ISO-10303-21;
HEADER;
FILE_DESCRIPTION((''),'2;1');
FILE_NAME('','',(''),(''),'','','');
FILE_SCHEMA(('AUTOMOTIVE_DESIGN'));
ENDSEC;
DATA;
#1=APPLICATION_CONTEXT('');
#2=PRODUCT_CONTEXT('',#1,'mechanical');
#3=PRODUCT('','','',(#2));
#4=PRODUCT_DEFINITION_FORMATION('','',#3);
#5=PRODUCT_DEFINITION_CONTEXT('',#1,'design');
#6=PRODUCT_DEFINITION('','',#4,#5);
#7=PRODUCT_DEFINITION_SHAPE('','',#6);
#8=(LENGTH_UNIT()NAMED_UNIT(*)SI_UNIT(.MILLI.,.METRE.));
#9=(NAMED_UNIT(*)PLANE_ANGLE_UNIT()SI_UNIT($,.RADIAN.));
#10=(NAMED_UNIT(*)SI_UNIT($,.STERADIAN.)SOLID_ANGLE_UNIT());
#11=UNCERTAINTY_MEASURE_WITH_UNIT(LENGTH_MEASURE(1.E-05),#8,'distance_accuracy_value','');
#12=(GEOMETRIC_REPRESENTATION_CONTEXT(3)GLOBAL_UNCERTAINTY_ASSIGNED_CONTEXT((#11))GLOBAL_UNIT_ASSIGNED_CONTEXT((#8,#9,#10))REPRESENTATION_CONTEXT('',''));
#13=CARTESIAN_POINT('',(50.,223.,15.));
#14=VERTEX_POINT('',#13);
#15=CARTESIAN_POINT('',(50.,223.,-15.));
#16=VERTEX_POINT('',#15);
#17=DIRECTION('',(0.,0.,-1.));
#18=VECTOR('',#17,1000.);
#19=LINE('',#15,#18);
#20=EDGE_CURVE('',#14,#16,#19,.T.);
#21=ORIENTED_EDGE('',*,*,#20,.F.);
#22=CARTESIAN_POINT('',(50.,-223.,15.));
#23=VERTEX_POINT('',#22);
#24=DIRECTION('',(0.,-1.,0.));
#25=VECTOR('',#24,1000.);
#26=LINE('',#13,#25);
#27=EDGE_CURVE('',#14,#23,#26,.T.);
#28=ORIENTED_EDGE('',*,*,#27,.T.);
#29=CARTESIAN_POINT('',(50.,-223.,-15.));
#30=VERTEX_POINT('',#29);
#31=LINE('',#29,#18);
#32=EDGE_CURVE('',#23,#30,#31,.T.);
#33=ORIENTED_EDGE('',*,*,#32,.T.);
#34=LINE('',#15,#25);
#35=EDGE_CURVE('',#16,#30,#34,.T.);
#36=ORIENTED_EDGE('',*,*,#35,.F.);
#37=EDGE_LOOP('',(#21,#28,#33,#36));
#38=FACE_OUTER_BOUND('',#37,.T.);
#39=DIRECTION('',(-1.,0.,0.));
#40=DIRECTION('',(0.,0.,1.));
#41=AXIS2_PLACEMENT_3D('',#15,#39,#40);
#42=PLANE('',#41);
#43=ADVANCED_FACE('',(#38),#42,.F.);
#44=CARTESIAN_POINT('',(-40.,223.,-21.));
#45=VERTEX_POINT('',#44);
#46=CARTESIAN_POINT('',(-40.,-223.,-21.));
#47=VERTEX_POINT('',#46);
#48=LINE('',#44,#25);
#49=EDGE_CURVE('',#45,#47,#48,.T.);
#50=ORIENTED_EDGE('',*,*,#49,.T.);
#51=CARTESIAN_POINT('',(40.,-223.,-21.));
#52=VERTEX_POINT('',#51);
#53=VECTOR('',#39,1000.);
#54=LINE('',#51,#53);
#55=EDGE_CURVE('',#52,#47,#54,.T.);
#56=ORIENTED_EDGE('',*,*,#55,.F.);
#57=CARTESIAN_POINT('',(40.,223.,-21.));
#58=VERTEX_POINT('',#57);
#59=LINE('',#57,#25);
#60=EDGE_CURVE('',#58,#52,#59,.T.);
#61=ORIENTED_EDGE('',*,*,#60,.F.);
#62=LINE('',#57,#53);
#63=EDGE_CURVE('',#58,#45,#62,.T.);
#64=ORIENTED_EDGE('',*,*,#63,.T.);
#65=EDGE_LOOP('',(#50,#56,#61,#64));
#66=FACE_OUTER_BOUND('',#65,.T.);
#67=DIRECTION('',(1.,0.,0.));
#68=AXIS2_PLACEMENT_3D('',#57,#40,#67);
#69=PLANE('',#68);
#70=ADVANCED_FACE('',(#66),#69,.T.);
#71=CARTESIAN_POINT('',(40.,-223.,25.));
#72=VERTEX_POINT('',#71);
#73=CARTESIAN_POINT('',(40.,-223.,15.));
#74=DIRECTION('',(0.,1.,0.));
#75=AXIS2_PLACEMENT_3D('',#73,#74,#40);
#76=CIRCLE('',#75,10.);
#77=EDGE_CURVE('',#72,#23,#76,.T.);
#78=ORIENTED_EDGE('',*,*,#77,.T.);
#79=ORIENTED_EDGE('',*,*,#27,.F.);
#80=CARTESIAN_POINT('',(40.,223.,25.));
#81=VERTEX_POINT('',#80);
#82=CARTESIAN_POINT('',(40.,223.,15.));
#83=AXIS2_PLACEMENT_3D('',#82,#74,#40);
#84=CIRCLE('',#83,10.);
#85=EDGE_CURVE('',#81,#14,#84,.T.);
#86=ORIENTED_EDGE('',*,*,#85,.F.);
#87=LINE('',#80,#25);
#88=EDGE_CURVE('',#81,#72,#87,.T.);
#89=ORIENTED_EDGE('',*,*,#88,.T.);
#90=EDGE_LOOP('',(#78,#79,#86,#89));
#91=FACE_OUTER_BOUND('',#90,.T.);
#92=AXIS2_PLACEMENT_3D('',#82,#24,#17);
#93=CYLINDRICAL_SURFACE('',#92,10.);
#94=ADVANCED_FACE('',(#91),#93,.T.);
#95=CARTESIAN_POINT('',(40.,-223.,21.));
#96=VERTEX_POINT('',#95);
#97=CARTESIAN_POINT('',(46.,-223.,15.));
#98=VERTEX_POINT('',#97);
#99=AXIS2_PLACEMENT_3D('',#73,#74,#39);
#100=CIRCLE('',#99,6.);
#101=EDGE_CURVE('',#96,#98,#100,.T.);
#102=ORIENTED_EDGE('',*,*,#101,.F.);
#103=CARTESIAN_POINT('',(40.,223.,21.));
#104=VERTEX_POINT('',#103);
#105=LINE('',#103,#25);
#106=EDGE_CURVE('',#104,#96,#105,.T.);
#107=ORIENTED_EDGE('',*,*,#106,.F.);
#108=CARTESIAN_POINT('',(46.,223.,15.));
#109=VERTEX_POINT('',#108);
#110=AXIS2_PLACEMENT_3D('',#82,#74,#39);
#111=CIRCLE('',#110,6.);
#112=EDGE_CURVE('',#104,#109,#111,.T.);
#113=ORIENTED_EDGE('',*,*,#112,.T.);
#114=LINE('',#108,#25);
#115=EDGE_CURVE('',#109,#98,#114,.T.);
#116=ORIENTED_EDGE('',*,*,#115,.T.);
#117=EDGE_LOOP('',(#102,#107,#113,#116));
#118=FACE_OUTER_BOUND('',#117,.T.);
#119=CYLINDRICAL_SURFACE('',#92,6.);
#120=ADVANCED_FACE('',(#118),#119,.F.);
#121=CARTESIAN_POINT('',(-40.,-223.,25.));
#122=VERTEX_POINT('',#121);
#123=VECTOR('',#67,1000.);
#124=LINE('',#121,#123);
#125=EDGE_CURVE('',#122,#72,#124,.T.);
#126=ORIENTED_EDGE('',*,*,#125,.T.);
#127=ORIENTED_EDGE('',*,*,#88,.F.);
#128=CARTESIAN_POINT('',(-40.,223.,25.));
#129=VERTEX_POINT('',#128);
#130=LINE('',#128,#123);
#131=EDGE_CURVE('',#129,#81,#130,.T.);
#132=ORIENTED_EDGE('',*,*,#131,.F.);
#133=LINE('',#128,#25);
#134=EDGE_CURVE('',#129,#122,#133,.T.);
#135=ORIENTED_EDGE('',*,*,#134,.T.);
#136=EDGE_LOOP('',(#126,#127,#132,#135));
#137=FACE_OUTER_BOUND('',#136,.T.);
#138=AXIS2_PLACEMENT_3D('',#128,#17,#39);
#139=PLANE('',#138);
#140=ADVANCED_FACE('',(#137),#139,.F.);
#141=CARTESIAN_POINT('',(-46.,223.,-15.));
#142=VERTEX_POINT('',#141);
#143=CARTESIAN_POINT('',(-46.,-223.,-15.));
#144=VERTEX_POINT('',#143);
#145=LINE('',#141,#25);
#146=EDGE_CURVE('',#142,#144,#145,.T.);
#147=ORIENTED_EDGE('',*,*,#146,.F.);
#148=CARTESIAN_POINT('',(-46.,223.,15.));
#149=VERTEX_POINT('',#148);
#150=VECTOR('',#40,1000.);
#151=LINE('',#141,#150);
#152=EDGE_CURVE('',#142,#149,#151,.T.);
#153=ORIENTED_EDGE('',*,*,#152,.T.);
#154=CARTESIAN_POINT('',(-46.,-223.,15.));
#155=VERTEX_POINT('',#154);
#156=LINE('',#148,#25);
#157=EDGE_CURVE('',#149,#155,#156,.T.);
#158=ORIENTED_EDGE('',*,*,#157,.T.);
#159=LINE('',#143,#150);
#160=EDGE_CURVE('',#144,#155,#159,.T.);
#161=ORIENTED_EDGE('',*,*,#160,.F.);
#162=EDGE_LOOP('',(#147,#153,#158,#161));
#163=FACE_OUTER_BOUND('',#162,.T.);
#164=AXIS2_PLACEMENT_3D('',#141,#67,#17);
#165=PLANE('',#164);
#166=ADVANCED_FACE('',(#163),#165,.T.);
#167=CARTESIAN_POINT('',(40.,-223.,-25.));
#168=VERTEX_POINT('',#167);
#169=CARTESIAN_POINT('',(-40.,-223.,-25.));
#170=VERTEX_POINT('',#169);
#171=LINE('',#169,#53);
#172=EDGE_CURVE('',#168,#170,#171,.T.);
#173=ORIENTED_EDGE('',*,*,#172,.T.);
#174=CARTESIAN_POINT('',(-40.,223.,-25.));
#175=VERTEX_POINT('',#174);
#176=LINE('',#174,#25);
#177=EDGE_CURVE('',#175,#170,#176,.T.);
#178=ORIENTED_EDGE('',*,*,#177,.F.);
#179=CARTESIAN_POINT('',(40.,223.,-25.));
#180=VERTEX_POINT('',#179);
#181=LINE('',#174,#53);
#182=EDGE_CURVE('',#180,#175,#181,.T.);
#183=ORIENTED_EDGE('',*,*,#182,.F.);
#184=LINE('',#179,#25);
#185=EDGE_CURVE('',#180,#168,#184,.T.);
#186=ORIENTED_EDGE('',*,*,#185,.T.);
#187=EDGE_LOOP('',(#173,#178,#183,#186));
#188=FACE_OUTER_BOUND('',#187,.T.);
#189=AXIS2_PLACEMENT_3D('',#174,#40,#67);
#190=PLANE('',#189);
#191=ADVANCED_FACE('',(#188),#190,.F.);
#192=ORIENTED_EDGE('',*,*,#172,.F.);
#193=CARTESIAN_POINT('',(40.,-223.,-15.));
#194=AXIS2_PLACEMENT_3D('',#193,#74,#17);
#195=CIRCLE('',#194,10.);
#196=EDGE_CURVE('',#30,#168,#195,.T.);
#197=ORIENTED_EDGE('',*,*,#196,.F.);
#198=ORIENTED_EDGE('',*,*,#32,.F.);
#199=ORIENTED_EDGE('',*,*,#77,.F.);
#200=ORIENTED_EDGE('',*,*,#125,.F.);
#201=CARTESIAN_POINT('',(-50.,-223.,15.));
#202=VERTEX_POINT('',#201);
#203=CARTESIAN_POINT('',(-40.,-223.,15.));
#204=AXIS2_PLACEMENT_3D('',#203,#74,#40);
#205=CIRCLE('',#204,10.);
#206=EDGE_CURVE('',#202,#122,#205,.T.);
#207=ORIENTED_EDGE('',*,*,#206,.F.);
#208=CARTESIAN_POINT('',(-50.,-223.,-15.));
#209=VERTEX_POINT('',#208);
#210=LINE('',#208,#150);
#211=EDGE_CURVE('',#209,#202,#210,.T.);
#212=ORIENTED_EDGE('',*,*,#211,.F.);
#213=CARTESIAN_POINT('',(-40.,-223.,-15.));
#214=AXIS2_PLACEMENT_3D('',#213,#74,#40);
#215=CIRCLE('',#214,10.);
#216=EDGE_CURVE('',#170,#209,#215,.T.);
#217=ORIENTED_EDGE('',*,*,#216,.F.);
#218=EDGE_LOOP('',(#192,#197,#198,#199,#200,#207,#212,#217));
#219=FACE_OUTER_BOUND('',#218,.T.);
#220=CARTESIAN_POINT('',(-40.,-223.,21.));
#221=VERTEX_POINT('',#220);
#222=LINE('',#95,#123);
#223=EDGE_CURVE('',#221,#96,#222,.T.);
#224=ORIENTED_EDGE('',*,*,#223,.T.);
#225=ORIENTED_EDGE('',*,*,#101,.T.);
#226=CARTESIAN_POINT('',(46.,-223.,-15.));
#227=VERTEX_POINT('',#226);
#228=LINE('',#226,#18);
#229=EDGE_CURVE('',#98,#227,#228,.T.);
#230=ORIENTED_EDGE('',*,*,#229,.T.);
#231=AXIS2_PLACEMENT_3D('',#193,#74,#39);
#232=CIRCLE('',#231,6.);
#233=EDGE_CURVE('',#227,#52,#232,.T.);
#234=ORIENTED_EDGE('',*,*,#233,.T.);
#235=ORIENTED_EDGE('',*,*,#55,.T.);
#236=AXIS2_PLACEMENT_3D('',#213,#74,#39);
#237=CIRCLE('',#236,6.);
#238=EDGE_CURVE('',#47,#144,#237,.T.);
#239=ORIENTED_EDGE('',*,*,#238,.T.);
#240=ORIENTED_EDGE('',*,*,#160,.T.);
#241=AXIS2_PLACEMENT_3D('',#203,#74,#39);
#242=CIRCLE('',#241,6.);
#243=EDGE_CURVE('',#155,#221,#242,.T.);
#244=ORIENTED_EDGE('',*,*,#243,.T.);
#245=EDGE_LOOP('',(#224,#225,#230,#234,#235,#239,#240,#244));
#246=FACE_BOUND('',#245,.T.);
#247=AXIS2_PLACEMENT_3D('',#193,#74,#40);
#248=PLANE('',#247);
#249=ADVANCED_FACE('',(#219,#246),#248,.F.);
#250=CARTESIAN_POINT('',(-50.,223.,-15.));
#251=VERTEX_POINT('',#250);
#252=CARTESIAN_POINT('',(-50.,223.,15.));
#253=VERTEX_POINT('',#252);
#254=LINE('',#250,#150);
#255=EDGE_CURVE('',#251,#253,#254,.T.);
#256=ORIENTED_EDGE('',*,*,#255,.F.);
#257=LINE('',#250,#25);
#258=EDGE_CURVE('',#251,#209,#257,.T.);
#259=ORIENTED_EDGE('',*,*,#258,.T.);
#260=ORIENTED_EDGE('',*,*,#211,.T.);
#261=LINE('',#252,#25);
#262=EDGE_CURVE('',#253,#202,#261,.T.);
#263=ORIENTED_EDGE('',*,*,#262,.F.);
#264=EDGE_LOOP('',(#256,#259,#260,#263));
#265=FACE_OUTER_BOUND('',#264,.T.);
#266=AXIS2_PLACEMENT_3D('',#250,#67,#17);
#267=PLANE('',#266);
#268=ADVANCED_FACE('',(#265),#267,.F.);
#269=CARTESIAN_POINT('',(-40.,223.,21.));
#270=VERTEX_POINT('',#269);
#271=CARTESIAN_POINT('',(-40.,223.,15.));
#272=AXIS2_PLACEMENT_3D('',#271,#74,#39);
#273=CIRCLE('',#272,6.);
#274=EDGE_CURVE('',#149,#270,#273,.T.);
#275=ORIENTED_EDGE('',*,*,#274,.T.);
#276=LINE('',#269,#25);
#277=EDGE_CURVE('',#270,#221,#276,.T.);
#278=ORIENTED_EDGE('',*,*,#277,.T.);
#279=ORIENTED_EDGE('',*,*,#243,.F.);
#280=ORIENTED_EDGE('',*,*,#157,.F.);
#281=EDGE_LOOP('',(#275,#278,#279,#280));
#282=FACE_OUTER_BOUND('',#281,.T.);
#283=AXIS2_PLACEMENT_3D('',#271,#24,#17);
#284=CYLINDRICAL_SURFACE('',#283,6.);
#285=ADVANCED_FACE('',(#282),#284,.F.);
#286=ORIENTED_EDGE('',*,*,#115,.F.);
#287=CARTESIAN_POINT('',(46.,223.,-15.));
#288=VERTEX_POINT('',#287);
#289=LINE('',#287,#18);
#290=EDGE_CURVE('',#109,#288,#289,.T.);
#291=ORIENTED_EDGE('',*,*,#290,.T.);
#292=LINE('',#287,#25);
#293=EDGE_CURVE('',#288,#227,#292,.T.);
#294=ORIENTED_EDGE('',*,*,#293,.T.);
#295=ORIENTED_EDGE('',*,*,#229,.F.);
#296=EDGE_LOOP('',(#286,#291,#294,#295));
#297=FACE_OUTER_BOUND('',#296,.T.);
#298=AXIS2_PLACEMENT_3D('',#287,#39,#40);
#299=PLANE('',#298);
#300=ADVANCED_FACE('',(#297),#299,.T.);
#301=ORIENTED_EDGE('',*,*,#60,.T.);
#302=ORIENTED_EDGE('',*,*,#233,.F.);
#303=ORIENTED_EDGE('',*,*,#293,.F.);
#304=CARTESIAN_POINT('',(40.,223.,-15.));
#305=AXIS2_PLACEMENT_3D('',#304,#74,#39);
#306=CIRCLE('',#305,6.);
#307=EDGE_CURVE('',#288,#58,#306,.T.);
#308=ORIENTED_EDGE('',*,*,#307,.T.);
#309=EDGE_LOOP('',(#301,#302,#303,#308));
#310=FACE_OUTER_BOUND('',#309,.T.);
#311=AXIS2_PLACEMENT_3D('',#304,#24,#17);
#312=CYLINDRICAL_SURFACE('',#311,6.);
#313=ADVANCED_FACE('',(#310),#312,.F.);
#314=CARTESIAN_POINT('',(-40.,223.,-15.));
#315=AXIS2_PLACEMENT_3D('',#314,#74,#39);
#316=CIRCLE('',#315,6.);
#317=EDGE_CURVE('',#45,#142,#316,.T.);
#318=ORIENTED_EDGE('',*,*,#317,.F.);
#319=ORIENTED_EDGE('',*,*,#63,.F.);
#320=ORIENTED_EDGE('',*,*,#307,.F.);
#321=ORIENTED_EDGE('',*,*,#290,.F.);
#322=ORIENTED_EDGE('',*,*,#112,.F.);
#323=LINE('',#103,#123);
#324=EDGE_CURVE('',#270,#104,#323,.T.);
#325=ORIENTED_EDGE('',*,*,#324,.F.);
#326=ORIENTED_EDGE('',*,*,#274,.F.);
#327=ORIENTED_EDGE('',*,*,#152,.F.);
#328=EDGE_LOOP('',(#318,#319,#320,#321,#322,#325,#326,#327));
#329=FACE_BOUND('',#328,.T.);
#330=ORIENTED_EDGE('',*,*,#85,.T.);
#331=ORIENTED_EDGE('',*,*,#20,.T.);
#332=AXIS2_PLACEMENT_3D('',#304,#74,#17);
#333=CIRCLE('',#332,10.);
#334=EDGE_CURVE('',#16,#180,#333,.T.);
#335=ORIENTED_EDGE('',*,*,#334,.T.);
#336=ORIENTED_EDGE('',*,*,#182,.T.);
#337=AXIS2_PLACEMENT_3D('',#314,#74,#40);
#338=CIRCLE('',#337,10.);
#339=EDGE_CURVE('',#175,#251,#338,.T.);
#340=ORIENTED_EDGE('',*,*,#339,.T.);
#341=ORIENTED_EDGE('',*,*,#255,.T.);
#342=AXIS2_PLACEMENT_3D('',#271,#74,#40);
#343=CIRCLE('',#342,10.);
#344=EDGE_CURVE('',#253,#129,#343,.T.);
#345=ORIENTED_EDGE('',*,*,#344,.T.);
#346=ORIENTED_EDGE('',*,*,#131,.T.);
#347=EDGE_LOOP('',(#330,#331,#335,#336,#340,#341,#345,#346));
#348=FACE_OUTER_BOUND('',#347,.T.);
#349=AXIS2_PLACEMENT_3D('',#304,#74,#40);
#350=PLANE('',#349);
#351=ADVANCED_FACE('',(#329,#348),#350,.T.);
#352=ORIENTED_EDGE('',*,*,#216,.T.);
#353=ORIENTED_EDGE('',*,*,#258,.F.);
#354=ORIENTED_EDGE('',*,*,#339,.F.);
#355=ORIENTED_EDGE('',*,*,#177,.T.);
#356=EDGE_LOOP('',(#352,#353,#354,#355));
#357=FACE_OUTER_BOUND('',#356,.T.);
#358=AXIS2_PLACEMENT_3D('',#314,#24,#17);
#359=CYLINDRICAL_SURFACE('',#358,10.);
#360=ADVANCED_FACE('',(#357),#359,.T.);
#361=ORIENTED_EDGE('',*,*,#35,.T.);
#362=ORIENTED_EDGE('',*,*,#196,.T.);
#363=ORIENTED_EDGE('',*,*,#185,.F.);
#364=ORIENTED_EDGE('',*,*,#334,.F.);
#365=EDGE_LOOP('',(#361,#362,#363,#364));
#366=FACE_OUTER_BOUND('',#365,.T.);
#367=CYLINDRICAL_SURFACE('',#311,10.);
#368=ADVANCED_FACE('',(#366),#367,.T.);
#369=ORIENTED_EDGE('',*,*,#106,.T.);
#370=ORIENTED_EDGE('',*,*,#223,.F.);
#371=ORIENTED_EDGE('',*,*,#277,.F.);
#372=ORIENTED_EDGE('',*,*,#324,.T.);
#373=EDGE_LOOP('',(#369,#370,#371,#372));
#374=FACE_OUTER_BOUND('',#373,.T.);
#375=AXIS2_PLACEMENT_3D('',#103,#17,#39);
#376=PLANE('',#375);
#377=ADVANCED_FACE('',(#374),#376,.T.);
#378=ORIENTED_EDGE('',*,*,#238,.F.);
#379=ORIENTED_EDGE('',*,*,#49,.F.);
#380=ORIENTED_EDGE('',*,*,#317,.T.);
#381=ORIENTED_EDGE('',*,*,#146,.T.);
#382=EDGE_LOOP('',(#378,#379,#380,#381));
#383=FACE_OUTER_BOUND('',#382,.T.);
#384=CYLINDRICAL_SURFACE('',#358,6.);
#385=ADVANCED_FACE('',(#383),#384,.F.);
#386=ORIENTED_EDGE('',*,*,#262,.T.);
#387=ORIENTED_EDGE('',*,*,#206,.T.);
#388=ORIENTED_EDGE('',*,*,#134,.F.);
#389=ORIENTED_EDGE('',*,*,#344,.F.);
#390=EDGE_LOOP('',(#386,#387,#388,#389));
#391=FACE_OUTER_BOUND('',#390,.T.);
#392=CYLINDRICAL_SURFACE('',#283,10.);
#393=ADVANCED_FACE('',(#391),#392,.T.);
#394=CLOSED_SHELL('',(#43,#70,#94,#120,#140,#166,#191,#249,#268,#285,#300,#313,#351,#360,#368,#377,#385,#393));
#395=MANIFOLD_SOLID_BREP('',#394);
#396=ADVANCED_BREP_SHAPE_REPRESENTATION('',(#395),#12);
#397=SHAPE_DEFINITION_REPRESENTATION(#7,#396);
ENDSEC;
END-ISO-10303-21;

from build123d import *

# Parameters (mm, degrees)
EXTRUDE_THIN1_DEPTH = 223


with BuildPart() as part:
    # Sketch1 → Extrude-Thin1 (new, symmetric)
    with BuildSketch(Plane(origin=(0, 0, 0), x_dir=(1, 0, 0), z_dir=(0, 1, 0))):
        with BuildLine():
            Line((-40, 25), (40, 25))
            ThreePointArc((40, 25), (47.071067812, 22.071067812), (50, 15))
            Line((50, 15), (50, -15))
            ThreePointArc((50, -15), (47.071067812, -22.071067812), (40, -25))
            Line((40, -25), (-40, -25))
            ThreePointArc((-40, -25), (-47.071067812, -22.071067812), (-50, -15))
            Line((-50, -15), (-50, 15))
            ThreePointArc((-50, 15), (-47.071067812, 22.071067812), (-40, 25))
        make_face()
        with BuildLine():
            Line((-40, 21), (40, 21))
            ThreePointArc((40, 21), (44.242640687, 19.242640687), (46, 15))
            Line((46, 15), (46, -15))
            ThreePointArc((46, -15), (44.242640687, -19.242640687), (40, -21))
            Line((40, -21), (-40, -21))
            ThreePointArc((-40, -21), (-44.242640687, -19.242640687), (-46, -15))
            Line((-46, -15), (-46, 15))
            ThreePointArc((-46, 15), (-44.242640687, 19.242640687), (-40, 21))
        make_face(mode=Mode.SUBTRACT)
    extrude(amount=EXTRUDE_THIN1_DEPTH, both=True)


solid = part.part
